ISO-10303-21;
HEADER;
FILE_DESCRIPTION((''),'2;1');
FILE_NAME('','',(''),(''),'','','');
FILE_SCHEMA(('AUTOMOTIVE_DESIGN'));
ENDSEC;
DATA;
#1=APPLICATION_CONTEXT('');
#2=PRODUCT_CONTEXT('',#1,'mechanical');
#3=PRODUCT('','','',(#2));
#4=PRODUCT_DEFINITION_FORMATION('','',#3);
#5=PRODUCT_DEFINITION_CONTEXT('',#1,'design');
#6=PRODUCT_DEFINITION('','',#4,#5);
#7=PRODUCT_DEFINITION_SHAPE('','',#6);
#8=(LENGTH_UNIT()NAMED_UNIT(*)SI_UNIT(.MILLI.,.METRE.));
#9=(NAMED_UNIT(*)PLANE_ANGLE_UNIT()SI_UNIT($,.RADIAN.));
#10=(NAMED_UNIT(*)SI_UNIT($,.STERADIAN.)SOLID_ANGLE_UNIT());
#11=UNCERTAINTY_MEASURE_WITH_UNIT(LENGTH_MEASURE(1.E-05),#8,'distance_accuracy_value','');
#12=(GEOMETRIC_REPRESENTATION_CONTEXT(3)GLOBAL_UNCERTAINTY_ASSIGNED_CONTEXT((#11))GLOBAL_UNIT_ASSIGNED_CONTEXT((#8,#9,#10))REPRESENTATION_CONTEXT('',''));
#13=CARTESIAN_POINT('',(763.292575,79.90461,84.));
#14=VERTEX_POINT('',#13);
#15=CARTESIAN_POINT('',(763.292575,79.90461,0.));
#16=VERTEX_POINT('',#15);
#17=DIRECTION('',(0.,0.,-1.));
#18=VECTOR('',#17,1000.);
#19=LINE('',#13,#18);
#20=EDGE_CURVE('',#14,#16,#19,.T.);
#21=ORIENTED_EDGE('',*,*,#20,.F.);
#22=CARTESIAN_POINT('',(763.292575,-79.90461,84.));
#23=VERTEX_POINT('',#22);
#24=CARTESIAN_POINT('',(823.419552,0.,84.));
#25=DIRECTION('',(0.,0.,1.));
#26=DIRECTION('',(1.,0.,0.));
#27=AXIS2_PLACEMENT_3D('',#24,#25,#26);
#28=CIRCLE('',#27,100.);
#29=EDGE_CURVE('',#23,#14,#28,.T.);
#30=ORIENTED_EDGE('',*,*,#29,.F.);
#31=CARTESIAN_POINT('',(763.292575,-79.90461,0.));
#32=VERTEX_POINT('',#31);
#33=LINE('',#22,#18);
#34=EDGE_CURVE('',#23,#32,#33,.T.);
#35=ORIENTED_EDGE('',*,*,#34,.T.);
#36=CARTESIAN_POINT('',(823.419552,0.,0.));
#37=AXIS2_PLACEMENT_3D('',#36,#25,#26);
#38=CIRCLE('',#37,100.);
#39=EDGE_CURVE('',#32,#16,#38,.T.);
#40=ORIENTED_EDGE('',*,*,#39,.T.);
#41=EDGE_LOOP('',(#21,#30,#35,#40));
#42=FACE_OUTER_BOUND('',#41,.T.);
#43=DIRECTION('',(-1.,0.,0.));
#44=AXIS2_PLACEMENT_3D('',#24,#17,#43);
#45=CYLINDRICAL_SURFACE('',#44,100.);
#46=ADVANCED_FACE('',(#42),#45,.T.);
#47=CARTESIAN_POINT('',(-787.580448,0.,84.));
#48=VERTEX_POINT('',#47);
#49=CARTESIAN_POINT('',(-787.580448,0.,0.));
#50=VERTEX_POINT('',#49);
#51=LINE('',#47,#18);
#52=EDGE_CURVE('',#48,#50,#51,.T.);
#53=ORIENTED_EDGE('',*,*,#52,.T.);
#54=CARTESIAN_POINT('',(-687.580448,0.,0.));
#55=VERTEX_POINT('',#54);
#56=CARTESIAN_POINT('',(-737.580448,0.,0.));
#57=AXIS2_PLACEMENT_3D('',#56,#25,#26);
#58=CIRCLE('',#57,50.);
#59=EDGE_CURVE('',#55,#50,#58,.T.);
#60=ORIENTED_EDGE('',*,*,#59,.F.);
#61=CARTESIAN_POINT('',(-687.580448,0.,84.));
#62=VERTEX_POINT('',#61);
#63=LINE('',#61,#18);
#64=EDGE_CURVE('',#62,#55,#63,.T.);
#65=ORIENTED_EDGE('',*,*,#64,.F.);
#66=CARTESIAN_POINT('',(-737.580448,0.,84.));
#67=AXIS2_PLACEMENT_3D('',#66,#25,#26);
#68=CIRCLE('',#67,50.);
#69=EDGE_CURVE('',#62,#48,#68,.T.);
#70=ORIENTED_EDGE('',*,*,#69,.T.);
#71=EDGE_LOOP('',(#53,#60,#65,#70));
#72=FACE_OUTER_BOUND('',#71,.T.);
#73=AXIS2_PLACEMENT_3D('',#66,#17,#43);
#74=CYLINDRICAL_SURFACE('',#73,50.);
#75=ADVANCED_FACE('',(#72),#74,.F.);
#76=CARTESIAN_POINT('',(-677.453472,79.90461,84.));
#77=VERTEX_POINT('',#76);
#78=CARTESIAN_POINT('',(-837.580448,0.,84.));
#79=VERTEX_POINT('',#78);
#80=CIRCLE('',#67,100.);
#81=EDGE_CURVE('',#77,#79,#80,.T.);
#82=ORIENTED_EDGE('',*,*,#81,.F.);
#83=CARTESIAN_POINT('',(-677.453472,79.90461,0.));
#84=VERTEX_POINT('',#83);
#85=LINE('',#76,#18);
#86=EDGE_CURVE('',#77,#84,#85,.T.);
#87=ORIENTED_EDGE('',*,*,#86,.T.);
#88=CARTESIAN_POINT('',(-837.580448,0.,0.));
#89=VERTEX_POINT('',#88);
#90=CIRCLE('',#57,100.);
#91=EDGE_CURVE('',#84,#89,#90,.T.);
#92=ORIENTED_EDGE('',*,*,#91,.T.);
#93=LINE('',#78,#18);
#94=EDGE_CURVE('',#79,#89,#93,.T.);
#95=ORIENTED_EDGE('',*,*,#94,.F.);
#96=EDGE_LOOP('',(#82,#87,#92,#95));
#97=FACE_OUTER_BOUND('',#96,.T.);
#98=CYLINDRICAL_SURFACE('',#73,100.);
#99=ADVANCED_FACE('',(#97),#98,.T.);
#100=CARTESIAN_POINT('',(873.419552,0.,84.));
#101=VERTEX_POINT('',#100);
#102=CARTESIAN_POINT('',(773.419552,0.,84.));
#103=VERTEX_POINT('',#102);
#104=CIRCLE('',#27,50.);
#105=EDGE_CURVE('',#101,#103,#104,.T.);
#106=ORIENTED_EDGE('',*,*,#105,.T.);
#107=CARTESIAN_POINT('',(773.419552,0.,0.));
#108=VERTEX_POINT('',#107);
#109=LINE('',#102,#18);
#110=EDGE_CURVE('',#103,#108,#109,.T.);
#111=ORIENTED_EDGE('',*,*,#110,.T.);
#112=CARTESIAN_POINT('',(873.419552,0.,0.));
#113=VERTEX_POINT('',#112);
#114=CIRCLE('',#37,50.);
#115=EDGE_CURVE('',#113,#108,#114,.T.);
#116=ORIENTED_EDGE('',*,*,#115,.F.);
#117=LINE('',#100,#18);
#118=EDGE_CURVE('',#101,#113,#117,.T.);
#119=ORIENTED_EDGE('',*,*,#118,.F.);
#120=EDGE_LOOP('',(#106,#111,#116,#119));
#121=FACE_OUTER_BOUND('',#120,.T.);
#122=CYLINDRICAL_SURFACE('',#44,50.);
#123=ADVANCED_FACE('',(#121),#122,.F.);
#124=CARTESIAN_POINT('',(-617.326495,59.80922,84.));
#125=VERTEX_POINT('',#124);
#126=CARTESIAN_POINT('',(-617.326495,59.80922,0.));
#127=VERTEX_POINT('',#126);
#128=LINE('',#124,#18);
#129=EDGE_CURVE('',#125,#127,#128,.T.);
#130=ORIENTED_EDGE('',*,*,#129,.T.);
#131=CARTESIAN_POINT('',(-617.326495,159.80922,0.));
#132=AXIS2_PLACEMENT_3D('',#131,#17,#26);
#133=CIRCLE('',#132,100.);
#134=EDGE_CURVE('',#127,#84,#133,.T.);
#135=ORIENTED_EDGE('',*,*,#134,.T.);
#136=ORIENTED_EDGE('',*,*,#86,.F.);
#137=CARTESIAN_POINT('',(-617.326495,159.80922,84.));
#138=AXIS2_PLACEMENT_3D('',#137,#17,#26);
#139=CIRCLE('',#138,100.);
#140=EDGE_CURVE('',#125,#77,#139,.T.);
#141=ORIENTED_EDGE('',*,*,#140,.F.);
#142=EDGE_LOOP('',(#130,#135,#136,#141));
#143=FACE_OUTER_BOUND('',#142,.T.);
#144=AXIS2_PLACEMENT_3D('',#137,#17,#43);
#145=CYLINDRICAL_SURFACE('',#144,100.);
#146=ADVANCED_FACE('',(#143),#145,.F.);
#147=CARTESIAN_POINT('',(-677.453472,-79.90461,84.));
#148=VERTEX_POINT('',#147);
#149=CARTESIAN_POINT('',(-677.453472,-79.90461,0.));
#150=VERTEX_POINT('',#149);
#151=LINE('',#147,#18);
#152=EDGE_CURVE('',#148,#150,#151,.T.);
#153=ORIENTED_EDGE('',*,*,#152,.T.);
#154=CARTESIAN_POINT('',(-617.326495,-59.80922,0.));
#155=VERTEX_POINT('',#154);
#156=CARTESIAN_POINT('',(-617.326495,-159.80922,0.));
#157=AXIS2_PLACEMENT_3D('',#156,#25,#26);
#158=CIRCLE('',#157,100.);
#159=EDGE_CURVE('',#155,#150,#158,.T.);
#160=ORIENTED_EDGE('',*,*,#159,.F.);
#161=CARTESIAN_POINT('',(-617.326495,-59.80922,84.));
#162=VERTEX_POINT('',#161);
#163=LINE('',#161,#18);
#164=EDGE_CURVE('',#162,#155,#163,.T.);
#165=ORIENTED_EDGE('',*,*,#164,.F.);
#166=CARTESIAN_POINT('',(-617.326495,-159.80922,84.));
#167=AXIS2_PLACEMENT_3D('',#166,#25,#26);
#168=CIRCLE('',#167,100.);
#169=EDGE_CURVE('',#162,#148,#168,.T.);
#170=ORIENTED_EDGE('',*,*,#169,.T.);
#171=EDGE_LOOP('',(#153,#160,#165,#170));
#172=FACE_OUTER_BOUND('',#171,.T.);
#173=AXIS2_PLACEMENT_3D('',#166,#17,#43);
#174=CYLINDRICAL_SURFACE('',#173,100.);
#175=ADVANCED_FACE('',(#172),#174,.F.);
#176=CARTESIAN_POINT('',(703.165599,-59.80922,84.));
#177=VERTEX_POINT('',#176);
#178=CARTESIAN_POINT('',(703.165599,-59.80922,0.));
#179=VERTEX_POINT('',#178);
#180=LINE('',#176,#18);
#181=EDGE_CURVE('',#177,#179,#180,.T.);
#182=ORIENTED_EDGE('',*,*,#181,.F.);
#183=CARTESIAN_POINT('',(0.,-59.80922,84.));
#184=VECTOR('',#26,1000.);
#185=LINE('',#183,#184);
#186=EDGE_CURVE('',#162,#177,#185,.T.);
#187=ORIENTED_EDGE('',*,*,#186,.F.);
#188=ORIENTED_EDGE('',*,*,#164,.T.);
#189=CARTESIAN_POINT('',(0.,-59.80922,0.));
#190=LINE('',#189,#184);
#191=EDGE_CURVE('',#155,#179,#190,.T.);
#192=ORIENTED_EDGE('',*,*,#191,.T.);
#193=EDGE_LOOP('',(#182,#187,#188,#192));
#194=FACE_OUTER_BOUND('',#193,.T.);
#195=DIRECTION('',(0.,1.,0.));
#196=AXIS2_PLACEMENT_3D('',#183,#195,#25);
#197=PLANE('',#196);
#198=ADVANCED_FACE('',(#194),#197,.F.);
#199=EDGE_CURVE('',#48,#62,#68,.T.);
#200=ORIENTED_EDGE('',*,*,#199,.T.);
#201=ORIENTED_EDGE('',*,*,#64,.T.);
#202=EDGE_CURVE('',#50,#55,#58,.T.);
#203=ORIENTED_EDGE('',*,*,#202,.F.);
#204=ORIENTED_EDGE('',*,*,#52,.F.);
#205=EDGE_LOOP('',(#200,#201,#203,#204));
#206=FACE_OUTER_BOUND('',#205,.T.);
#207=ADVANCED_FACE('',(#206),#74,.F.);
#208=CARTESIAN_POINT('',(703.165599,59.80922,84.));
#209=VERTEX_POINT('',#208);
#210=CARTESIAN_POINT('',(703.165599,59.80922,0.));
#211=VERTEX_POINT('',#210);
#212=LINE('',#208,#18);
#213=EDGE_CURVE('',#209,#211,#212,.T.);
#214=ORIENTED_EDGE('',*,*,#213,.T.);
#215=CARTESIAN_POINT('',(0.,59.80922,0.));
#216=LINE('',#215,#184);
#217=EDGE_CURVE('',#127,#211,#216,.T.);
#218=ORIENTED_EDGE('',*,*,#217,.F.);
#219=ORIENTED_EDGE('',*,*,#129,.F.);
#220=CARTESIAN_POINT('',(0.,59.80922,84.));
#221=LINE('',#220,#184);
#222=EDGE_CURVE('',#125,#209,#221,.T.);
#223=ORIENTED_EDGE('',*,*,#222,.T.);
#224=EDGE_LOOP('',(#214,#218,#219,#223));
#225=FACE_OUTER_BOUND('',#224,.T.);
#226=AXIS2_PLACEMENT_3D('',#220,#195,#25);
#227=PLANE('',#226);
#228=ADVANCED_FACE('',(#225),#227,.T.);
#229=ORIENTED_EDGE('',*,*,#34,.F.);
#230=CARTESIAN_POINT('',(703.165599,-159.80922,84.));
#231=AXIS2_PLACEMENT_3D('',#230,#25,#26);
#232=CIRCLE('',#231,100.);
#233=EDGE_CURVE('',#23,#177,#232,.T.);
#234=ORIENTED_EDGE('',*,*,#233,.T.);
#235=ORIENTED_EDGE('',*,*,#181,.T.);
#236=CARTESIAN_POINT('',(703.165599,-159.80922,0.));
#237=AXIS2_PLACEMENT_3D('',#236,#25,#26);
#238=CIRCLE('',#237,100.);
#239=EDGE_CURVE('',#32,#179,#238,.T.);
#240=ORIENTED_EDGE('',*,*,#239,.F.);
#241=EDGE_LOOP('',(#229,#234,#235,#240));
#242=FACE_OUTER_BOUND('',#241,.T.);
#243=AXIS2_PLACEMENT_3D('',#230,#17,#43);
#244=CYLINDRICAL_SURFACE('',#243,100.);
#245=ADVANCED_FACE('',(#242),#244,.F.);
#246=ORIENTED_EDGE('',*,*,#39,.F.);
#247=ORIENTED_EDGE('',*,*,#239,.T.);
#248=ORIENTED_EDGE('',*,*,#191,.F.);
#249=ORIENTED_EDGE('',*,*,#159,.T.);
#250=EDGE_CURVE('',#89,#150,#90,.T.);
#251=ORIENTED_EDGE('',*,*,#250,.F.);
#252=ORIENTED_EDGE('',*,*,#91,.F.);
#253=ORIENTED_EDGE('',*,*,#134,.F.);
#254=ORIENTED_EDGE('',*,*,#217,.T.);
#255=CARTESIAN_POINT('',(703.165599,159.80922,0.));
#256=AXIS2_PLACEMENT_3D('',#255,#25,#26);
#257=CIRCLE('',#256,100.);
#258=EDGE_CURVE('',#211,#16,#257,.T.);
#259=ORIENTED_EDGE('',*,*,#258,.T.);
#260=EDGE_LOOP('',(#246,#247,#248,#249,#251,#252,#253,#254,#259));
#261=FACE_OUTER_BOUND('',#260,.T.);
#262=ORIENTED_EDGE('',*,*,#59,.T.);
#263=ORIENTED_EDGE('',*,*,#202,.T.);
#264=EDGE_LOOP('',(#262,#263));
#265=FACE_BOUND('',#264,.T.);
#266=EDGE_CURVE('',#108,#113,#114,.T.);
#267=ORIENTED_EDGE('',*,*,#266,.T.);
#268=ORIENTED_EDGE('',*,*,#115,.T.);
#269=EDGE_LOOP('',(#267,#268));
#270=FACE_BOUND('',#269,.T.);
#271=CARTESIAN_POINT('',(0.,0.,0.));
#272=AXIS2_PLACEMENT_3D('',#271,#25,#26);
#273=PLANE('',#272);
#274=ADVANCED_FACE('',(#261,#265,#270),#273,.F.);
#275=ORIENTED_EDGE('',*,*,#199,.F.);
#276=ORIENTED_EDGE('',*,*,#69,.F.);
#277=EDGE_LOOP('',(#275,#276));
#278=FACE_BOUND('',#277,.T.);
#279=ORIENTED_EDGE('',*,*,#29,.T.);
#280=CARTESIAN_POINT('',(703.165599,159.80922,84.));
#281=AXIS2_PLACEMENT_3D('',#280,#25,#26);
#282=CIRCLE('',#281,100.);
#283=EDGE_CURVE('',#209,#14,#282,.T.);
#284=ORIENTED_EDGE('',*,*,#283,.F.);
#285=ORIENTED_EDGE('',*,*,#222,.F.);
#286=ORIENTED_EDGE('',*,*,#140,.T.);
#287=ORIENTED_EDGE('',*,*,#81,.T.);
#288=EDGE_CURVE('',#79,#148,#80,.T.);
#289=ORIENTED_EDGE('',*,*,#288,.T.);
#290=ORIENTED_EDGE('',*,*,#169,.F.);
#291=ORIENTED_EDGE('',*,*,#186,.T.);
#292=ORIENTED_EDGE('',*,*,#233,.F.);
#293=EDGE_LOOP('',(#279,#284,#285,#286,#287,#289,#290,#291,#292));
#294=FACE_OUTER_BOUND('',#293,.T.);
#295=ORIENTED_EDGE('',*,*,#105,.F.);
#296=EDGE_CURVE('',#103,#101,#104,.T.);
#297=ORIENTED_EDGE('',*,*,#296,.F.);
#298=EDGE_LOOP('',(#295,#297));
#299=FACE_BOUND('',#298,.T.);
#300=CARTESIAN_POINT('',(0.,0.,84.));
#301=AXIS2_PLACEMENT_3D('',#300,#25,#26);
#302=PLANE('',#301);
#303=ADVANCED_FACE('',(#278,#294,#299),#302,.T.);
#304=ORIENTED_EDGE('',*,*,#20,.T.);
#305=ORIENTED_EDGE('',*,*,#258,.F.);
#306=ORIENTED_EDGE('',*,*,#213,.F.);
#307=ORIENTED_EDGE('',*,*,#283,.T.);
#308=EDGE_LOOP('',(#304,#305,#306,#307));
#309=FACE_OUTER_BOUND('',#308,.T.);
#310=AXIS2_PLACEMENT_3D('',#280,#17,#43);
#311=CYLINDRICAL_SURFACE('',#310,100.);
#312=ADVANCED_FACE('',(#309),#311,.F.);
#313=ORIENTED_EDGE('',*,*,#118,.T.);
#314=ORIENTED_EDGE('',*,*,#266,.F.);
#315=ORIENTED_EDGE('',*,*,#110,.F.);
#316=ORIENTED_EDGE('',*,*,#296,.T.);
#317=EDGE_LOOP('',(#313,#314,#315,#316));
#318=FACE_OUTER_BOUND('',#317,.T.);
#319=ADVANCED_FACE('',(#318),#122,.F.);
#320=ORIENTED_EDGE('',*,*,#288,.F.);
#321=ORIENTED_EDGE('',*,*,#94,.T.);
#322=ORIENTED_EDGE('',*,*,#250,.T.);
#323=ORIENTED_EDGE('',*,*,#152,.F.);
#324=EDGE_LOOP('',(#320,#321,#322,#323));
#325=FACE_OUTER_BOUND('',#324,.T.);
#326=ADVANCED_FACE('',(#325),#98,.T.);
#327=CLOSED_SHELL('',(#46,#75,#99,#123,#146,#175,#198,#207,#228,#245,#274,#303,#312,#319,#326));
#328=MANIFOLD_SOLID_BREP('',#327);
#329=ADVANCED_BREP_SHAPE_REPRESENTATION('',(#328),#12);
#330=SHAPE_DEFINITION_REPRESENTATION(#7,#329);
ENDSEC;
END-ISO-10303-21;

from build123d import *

# Parameters (mm, degrees)
SKETCH1_R           = 50
BOSS_EXTRUDE1_DEPTH = 84


with BuildPart() as part:
    # Sketch1 → Boss-Extrude1 (new body)
    with BuildSketch(Plane.XY):
        with BuildLine():
            Line((-617.326495153, 59.809220037), (703.165599022, 59.809220037))
            ThreePointArc((703.165599022, 59.809220037), (734.86369832, 64.966031031), (763.292575479, 79.904610019))
            ThreePointArc((763.292575479, 79.904610019), (923.419551935, 0), (763.292575479, -79.904610019))
            ThreePointArc((763.292575479, -79.904610019), (734.86369832, -64.966031031), (703.165599022, -59.809220037))
            Line((703.165599022, -59.809220037), (-617.326495153, -59.809220037))
            ThreePointArc((-617.326495153, -59.809220037), (-649.02459445, -64.966031031), (-677.453471609, -79.904610019))
            ThreePointArc((-677.453471609, -79.904610019), (-837.580448065, 0), (-677.453471609, 79.904610019))
            ThreePointArc((-677.453471609, 79.904610019), (-649.02459445, 64.966031031), (-617.326495153, 59.809220037))
        make_face()
        with Locations(Location((-737.580448065, 0, 0), (0, 0, 180))):
            Circle(SKETCH1_R, mode=Mode.SUBTRACT)
        with Locations(Location((823.419551935, 0, 0), (0, 0, 180))):
            Circle(SKETCH1_R, mode=Mode.SUBTRACT)
    extrude(amount=BOSS_EXTRUDE1_DEPTH)


solid = part.part
